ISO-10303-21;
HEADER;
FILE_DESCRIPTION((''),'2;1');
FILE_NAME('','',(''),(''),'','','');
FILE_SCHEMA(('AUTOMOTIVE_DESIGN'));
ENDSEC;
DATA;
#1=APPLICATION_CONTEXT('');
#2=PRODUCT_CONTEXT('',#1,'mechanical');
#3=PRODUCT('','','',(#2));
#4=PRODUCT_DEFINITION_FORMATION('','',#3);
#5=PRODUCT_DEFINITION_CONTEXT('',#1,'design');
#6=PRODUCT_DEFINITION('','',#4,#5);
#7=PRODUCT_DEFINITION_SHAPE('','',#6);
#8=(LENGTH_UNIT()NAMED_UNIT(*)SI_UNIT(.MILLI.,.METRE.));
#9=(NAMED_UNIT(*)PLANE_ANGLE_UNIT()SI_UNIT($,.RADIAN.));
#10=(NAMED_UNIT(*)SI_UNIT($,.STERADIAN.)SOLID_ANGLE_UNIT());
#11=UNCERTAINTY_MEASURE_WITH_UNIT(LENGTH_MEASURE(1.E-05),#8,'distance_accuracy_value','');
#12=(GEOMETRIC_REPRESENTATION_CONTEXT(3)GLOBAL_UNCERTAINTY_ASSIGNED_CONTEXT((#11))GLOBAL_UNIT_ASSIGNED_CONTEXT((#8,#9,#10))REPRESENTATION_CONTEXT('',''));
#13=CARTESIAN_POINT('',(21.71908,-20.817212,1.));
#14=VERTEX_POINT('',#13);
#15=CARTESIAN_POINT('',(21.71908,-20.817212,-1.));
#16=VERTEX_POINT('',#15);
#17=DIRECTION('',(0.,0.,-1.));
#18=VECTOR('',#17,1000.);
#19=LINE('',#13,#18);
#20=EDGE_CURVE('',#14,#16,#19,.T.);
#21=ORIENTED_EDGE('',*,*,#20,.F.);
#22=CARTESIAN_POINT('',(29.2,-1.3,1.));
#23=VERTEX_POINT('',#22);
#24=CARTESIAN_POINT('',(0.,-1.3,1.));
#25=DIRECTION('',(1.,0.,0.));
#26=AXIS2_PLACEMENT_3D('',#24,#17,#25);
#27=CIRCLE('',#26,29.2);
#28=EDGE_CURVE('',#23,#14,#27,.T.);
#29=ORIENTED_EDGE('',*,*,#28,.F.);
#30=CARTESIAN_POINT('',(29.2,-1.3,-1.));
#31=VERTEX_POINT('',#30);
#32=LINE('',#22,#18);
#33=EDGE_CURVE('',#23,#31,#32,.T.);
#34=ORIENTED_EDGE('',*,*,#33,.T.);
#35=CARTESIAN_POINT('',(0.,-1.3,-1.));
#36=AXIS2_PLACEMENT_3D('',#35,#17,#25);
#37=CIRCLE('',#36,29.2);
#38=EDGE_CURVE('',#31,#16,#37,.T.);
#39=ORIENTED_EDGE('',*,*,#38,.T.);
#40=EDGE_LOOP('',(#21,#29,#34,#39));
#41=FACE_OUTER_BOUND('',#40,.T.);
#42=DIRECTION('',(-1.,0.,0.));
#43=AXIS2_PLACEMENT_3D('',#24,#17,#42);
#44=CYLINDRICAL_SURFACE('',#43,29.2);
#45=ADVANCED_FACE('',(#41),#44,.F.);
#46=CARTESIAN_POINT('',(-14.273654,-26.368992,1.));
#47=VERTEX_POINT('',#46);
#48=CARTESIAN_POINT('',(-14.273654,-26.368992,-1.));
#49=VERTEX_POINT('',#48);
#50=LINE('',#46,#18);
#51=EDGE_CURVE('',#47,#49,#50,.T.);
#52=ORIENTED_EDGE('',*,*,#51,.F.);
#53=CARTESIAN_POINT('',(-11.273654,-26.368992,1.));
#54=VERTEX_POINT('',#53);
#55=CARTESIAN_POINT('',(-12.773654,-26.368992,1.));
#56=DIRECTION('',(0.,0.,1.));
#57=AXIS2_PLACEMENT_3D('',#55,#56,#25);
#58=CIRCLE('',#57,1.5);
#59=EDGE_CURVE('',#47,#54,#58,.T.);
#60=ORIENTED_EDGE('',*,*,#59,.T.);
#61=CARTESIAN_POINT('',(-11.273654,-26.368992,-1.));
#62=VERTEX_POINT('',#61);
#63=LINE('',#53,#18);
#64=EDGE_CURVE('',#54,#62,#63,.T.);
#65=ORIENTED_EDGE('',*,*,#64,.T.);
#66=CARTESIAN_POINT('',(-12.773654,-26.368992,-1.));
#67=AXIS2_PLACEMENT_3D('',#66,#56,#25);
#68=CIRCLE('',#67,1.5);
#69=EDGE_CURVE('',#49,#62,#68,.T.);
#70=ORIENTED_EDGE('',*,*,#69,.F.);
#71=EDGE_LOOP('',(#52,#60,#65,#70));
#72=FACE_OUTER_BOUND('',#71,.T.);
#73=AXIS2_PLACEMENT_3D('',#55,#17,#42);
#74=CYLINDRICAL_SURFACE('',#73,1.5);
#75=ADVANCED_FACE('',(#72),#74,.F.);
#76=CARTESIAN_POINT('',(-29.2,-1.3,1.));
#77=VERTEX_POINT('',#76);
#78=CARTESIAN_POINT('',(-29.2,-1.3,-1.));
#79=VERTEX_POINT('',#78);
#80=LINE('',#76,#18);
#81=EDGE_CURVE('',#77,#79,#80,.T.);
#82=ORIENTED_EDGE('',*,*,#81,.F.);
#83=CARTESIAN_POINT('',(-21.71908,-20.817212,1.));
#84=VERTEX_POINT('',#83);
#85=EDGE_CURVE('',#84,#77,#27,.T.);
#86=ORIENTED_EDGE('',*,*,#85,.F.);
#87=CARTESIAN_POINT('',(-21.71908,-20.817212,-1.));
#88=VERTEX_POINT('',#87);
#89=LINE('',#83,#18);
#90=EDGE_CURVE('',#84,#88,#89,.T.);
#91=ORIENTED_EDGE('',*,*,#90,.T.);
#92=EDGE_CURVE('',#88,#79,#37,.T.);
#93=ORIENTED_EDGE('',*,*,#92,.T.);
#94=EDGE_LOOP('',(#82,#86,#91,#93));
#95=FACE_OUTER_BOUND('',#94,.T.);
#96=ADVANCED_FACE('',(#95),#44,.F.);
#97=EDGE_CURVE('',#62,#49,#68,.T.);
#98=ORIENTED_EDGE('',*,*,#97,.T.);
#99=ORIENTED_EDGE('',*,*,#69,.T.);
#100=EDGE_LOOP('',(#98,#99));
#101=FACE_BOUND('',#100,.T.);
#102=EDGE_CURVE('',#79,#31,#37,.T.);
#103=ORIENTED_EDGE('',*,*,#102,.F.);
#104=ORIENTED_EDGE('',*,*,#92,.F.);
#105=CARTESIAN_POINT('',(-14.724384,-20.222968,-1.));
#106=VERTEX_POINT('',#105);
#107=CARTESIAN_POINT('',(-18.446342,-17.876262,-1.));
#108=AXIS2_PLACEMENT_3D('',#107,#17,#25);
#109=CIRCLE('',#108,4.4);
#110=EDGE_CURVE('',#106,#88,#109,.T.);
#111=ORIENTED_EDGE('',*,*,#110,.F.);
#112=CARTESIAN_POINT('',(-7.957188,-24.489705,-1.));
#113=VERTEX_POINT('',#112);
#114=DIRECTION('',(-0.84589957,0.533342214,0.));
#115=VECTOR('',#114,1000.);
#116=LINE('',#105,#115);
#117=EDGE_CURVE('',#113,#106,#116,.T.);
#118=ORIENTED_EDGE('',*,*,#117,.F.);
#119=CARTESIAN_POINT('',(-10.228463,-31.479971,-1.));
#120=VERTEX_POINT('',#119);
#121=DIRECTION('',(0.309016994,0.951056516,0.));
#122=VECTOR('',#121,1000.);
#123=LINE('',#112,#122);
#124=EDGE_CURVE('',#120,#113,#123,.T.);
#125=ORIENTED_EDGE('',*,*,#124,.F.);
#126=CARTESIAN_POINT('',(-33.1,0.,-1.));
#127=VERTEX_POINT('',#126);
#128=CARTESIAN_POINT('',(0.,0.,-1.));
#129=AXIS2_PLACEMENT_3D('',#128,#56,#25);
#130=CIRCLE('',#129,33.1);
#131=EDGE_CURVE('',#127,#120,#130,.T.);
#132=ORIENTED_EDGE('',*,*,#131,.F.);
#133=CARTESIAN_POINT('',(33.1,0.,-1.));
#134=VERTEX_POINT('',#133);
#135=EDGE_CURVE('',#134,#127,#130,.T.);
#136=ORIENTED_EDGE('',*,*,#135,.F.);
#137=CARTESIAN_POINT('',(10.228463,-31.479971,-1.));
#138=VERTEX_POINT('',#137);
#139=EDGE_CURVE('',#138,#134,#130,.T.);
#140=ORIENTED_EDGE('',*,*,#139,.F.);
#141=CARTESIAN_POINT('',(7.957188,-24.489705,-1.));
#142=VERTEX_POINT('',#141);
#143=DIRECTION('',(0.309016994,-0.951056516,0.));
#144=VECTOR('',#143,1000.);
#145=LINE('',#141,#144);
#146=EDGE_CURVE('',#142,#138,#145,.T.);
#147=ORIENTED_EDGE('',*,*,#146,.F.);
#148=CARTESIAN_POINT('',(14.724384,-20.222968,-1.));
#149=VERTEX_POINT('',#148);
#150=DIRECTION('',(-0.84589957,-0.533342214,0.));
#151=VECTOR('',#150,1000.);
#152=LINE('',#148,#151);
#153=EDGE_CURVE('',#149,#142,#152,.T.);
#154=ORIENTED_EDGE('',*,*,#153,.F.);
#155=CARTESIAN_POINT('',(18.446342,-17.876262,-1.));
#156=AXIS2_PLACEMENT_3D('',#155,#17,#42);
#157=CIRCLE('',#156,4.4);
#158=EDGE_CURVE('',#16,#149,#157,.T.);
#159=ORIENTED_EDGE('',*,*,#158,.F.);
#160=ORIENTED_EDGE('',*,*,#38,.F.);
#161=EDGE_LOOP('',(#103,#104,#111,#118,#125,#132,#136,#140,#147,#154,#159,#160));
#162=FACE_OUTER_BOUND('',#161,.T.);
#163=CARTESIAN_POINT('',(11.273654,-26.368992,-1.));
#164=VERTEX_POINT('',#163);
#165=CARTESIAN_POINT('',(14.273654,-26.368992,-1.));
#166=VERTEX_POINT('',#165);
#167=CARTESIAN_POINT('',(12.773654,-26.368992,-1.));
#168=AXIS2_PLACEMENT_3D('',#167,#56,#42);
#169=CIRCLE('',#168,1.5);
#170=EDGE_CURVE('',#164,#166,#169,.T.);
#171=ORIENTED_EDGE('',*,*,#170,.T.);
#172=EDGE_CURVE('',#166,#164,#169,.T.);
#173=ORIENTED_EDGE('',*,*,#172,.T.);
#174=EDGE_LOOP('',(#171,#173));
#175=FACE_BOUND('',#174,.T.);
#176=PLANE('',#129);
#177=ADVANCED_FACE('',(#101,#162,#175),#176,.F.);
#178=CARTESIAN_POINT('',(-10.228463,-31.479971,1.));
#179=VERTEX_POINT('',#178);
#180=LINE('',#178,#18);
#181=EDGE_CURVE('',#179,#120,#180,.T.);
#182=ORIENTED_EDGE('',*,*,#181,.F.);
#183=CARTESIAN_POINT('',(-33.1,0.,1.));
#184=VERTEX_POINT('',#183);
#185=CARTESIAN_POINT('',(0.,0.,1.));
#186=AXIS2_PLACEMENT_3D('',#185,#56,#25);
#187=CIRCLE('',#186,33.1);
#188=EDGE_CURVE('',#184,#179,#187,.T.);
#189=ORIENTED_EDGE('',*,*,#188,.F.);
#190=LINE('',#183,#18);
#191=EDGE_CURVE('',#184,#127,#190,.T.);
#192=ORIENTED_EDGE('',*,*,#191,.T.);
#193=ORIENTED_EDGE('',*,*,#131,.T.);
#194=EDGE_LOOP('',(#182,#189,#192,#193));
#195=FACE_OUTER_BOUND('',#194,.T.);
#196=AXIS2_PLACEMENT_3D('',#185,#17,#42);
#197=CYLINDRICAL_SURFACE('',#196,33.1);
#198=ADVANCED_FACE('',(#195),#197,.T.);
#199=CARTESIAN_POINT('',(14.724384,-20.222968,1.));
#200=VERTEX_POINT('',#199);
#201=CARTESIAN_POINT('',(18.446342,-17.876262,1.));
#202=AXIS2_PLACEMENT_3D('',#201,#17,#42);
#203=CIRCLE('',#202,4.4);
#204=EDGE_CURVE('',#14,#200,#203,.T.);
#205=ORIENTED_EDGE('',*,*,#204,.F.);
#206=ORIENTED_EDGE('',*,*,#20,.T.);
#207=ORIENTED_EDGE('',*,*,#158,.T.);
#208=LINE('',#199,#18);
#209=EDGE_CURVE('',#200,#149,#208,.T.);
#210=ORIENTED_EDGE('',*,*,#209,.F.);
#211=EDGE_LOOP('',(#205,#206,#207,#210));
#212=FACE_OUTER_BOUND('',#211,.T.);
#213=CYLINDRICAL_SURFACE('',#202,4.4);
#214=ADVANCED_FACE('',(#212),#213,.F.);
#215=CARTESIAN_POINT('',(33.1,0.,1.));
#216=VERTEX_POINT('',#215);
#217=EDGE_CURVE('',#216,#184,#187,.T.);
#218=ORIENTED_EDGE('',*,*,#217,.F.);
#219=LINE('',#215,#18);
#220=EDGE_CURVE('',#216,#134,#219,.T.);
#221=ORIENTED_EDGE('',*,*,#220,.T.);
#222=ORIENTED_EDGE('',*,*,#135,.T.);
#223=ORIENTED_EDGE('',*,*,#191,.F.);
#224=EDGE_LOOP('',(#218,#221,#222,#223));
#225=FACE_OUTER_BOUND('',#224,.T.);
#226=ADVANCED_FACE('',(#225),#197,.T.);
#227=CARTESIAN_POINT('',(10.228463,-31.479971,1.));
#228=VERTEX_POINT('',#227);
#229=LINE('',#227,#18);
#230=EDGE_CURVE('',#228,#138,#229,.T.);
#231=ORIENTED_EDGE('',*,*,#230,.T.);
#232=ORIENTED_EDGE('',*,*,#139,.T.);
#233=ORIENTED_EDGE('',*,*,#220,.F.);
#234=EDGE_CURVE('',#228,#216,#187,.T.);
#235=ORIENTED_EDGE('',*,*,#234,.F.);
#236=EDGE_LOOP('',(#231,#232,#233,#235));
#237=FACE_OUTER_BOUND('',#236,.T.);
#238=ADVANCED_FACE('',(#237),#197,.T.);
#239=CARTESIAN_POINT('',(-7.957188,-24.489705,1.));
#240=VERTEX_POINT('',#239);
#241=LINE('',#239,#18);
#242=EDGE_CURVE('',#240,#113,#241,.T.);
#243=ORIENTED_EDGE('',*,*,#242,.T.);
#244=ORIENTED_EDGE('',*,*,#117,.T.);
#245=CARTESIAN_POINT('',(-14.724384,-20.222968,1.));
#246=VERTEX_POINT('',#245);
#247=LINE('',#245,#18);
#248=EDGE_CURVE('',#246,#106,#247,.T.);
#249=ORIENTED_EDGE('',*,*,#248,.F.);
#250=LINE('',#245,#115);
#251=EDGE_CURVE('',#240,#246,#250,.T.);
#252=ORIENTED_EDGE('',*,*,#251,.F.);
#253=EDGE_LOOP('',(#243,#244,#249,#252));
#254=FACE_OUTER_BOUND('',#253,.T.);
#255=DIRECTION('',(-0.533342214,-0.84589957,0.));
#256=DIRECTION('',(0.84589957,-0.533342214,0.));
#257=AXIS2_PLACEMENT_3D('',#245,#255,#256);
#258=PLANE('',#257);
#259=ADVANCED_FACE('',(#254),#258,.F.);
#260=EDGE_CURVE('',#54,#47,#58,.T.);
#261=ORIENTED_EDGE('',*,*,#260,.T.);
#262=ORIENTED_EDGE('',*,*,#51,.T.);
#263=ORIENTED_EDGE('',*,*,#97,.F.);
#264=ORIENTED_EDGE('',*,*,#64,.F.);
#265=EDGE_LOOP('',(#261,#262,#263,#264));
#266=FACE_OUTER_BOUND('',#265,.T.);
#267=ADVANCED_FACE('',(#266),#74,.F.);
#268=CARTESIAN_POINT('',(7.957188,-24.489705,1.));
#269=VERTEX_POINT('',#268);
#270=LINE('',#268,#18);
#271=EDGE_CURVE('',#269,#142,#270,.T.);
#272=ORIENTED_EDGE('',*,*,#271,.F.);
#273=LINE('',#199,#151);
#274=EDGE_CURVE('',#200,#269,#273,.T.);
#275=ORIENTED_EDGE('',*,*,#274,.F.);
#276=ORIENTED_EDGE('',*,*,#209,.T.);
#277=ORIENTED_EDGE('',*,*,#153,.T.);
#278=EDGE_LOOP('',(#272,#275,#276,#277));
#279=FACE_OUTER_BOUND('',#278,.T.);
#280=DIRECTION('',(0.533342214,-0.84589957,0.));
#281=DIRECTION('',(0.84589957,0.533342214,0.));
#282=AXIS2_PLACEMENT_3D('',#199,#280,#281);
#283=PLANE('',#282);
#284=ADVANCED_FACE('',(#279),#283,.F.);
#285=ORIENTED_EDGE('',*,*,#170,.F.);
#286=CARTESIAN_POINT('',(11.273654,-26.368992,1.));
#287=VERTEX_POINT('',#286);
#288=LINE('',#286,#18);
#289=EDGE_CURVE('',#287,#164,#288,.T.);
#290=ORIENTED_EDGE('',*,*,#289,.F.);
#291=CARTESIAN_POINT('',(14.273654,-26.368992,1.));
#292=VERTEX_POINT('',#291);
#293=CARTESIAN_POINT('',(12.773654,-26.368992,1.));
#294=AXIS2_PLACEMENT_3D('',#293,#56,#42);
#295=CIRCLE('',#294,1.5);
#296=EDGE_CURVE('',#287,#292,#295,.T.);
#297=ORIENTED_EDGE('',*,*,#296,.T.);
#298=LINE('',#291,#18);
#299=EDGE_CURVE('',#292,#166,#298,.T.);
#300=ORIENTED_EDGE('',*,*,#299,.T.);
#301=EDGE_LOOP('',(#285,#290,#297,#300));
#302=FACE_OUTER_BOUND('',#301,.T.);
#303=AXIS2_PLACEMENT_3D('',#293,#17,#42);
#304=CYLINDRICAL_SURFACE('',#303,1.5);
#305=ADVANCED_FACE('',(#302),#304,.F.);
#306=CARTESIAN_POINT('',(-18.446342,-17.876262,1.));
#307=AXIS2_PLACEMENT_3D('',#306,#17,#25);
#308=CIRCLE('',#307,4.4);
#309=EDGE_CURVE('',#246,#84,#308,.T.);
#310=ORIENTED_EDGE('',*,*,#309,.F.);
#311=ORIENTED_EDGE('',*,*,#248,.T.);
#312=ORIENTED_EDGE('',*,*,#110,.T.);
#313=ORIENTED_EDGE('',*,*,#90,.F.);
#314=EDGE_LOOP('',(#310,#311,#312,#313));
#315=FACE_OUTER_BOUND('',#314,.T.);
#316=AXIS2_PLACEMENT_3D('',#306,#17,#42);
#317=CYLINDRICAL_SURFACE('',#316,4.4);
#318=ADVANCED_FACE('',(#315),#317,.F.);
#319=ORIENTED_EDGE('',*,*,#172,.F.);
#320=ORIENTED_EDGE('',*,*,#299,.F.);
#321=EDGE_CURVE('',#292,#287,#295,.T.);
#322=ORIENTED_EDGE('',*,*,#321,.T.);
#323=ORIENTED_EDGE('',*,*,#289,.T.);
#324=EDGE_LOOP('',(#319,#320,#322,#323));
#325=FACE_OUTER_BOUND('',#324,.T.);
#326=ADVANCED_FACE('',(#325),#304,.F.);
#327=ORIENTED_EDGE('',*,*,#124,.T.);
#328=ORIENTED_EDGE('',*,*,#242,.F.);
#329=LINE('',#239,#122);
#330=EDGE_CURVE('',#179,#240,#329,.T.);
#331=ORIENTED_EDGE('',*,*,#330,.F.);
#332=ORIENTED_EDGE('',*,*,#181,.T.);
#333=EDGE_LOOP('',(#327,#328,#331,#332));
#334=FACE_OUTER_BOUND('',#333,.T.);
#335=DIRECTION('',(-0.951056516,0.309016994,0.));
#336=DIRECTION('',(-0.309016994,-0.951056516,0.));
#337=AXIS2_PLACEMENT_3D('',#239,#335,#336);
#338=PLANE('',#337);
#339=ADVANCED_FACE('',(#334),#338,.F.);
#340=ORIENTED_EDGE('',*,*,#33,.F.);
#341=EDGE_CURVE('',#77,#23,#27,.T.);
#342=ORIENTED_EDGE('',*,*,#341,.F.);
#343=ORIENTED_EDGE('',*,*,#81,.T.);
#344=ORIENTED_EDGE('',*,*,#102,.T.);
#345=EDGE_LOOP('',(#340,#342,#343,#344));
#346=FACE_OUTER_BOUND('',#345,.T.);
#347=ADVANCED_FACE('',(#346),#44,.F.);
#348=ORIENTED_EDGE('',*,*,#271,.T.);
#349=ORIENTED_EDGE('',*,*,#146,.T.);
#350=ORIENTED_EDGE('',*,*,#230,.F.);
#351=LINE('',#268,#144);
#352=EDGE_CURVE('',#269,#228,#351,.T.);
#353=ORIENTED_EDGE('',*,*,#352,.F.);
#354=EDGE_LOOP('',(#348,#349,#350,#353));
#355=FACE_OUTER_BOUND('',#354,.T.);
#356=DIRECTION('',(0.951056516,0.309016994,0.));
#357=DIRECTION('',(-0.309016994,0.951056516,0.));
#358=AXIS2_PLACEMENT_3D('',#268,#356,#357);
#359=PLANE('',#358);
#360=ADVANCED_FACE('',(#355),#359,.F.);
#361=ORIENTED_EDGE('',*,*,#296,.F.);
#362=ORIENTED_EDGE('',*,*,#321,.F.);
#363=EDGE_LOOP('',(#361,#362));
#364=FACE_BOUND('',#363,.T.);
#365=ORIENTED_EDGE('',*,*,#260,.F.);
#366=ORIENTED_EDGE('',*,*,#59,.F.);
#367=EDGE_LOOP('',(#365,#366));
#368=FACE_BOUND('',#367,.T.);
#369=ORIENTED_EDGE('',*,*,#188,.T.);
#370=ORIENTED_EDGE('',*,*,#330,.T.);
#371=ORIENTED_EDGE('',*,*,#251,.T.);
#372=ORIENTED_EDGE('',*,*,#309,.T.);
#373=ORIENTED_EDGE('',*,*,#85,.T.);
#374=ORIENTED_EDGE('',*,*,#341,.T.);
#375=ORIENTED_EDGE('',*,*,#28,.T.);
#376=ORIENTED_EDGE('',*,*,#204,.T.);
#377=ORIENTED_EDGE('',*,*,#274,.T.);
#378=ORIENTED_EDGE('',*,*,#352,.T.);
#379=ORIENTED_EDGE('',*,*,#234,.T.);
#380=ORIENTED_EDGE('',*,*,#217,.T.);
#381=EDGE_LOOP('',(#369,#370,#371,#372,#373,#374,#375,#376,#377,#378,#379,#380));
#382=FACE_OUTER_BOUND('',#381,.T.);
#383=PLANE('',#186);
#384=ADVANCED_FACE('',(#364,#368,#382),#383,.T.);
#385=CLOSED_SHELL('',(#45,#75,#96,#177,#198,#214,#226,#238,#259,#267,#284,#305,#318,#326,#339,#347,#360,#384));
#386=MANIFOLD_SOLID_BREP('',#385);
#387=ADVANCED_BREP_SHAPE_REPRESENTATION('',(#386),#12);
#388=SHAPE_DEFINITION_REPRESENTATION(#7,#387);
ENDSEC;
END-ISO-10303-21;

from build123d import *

# Parameters (mm, degrees)
BASE_EXTRUDE_DEPTH      = 1
BASE_EXTRUDE_DEPTH_BACK = 1
SKETCH1_R               = 1.5


with BuildPart() as part:
    # Sketch1 → Base-Extrude (new, two sides: drawn at the far end of the back side and taken through both)
    with BuildSketch(Plane.XY.offset(-BASE_EXTRUDE_DEPTH_BACK)):
        with BuildLine():
            Line((-14.724384167, -20.222967583), (-7.957187605, -24.489705295))
            Line((-7.957187605, -24.489705295), (-10.228462514, -31.479970689))
            ThreePointArc((-10.228462514, -31.479970689), (0, 33.1), (10.228462514, -31.479970689))
            Line((10.228462514, -31.479970689), (7.957187605, -24.489705295))
            Line((7.957187605, -24.489705295), (14.724384167, -20.222967583))
            ThreePointArc((14.724384167, -20.222967583), (18.073876023, -22.260468599), (21.719080421, -20.817211524))
            ThreePointArc((21.719080421, -20.817211524), (0, 27.9), (-21.719080421, -20.817211524))
            ThreePointArc((-21.719080421, -20.817211524), (-18.073876023, -22.260468599), (-14.724384167, -20.222967583))
        make_face()
        with Locations((-12.773653929, -26.368992497)):
            Circle(SKETCH1_R, mode=Mode.SUBTRACT)
        with Locations(Location((12.773653929, -26.368992497, 0), (0, 0, 180))):
            Circle(SKETCH1_R, mode=Mode.SUBTRACT)
    extrude(amount=BASE_EXTRUDE_DEPTH + BASE_EXTRUDE_DEPTH_BACK)


solid = part.part
